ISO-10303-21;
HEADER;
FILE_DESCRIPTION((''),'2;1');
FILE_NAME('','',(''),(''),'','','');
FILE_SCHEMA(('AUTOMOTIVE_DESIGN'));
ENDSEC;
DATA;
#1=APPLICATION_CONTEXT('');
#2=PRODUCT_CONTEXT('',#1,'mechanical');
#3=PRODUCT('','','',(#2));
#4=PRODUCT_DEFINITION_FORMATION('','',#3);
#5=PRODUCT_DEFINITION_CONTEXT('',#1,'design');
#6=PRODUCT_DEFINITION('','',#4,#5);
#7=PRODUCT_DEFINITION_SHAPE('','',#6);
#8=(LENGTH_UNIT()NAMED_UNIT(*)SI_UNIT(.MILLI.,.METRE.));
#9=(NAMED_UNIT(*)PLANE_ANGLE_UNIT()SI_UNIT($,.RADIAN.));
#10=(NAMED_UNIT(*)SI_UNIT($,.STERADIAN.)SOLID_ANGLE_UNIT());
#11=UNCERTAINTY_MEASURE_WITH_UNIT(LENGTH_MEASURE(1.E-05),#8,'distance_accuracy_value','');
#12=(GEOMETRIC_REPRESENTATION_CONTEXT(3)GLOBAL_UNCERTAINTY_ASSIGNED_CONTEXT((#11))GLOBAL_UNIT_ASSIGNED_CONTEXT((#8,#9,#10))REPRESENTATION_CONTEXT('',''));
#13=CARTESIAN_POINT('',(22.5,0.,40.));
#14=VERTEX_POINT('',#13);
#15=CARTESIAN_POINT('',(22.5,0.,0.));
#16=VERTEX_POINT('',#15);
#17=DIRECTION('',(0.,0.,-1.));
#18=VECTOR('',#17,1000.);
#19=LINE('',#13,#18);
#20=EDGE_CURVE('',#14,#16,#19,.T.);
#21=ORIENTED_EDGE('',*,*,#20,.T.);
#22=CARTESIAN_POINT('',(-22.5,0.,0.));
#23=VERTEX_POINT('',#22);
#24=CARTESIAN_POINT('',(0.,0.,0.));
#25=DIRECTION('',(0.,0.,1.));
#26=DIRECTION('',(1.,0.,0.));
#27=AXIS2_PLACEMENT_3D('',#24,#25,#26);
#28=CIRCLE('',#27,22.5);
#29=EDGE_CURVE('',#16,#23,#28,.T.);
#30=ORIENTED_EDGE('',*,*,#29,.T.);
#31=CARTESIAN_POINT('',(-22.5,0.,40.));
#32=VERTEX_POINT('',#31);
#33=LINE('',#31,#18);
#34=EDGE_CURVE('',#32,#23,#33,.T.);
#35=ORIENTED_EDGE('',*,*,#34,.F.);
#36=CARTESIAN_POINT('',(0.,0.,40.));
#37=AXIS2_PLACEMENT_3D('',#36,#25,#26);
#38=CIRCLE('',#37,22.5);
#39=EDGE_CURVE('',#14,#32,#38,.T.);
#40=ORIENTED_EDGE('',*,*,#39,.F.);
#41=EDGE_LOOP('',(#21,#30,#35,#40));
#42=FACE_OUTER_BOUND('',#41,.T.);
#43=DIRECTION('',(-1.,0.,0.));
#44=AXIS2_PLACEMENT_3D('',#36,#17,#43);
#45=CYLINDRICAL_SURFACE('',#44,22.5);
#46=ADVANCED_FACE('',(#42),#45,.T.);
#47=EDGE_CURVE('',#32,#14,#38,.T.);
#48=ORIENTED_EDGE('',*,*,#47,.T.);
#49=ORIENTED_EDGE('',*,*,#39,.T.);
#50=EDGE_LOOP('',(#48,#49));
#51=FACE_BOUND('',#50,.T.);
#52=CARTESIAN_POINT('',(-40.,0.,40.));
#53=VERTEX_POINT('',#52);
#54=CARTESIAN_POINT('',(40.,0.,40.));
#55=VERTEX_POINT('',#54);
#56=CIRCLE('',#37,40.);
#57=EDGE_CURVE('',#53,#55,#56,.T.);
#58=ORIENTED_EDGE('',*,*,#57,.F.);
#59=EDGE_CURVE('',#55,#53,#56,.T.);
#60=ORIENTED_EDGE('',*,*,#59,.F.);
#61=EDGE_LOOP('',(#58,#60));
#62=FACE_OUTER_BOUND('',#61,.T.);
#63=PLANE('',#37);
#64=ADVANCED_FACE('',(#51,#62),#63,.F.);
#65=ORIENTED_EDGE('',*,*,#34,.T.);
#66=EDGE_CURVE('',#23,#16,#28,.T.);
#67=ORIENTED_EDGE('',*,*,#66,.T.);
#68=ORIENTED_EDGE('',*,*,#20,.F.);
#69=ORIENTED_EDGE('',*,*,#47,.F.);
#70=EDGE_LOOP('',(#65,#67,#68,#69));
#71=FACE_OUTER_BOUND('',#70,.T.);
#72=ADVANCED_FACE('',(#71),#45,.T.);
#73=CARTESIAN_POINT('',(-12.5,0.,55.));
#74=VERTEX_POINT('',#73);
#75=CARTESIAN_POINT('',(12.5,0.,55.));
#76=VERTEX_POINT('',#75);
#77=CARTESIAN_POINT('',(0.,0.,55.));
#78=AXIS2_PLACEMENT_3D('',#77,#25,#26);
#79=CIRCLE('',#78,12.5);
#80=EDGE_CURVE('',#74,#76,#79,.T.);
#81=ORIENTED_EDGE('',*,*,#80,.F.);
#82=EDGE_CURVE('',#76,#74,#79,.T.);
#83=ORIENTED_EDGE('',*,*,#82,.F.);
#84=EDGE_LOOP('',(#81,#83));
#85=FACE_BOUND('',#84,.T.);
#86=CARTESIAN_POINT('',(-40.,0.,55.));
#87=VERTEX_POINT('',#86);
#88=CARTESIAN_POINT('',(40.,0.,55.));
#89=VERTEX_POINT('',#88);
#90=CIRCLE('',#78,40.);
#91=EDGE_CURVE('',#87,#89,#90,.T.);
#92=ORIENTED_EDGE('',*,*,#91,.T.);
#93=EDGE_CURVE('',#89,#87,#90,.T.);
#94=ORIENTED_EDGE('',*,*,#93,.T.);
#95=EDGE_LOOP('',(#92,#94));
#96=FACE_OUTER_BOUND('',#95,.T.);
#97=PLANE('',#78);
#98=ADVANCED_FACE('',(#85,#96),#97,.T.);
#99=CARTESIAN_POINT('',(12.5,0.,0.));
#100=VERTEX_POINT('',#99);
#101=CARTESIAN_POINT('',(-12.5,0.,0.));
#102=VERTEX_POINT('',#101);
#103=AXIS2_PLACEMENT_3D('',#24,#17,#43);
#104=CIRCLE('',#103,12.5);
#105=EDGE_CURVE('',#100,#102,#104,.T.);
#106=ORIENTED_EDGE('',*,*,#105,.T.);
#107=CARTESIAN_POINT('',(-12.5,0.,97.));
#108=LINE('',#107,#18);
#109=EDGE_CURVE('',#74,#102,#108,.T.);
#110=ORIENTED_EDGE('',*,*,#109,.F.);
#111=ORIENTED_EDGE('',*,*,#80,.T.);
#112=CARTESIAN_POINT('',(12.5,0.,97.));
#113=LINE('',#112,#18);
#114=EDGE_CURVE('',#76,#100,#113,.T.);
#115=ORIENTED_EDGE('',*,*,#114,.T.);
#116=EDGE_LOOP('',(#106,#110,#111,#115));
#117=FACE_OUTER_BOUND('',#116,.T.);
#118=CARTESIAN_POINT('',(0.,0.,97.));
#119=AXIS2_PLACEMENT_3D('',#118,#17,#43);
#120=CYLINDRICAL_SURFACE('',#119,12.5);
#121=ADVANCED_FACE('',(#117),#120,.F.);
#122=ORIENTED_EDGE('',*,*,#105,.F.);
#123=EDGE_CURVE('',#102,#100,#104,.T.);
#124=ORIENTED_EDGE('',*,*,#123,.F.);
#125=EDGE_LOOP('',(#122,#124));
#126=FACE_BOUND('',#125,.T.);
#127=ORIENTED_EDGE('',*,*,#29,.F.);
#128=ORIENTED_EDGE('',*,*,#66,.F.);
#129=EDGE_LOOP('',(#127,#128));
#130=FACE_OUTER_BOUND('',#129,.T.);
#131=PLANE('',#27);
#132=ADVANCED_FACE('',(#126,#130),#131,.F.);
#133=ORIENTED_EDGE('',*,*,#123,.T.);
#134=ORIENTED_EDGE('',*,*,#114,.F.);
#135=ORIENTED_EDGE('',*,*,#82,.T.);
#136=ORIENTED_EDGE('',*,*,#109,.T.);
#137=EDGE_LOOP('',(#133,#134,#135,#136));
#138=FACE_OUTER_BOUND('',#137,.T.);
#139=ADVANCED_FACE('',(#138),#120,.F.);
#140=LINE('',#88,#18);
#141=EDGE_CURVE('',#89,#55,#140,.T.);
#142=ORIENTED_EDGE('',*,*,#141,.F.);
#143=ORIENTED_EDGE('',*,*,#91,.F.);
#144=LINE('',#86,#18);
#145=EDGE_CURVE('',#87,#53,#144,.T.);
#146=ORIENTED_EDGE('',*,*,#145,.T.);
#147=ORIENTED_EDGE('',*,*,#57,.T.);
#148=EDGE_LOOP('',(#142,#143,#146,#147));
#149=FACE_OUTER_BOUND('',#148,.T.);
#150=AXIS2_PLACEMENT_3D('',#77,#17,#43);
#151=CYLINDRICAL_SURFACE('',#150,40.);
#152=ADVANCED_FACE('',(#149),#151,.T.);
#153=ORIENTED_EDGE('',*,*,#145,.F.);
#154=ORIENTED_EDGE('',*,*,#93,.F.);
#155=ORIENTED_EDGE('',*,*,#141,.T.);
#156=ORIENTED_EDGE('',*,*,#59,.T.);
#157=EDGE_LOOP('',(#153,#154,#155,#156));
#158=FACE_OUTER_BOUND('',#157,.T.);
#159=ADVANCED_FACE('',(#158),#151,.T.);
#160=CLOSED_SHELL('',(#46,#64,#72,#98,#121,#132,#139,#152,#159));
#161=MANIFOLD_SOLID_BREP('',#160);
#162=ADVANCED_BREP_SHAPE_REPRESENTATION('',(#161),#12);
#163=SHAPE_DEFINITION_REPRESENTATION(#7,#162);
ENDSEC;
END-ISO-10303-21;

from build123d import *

# Parameters (mm, degrees)
SKETCH1_R           = 22.5
BOSS_EXTRUDE1_DEPTH = 40
SKETCH2_R           = 40
BOSS_EXTRUDE2_DEPTH = 15
SKETCH3_R           = 12.5
CUT_EXTRUDE1_DEPTH  = 97


with BuildPart() as part:
    # Sketch1 → Boss-Extrude1 (new body)
    with BuildSketch(Plane.XY):
        Circle(SKETCH1_R)
    extrude(amount=BOSS_EXTRUDE1_DEPTH)

    # Sketch2 → Boss-Extrude2 (add)
    with BuildSketch(Plane.XY.offset(40)):
        Circle(SKETCH2_R)
    extrude(amount=BOSS_EXTRUDE2_DEPTH)

    # Sketch3 → Cut-Extrude1 (cut)
    with BuildSketch(Plane(origin=(0, 0, 0), x_dir=(-1, 0, 0), z_dir=(0, 0, -1))):
        Circle(SKETCH3_R)
    extrude(amount=-CUT_EXTRUDE1_DEPTH, mode=Mode.SUBTRACT)


solid = part.part
